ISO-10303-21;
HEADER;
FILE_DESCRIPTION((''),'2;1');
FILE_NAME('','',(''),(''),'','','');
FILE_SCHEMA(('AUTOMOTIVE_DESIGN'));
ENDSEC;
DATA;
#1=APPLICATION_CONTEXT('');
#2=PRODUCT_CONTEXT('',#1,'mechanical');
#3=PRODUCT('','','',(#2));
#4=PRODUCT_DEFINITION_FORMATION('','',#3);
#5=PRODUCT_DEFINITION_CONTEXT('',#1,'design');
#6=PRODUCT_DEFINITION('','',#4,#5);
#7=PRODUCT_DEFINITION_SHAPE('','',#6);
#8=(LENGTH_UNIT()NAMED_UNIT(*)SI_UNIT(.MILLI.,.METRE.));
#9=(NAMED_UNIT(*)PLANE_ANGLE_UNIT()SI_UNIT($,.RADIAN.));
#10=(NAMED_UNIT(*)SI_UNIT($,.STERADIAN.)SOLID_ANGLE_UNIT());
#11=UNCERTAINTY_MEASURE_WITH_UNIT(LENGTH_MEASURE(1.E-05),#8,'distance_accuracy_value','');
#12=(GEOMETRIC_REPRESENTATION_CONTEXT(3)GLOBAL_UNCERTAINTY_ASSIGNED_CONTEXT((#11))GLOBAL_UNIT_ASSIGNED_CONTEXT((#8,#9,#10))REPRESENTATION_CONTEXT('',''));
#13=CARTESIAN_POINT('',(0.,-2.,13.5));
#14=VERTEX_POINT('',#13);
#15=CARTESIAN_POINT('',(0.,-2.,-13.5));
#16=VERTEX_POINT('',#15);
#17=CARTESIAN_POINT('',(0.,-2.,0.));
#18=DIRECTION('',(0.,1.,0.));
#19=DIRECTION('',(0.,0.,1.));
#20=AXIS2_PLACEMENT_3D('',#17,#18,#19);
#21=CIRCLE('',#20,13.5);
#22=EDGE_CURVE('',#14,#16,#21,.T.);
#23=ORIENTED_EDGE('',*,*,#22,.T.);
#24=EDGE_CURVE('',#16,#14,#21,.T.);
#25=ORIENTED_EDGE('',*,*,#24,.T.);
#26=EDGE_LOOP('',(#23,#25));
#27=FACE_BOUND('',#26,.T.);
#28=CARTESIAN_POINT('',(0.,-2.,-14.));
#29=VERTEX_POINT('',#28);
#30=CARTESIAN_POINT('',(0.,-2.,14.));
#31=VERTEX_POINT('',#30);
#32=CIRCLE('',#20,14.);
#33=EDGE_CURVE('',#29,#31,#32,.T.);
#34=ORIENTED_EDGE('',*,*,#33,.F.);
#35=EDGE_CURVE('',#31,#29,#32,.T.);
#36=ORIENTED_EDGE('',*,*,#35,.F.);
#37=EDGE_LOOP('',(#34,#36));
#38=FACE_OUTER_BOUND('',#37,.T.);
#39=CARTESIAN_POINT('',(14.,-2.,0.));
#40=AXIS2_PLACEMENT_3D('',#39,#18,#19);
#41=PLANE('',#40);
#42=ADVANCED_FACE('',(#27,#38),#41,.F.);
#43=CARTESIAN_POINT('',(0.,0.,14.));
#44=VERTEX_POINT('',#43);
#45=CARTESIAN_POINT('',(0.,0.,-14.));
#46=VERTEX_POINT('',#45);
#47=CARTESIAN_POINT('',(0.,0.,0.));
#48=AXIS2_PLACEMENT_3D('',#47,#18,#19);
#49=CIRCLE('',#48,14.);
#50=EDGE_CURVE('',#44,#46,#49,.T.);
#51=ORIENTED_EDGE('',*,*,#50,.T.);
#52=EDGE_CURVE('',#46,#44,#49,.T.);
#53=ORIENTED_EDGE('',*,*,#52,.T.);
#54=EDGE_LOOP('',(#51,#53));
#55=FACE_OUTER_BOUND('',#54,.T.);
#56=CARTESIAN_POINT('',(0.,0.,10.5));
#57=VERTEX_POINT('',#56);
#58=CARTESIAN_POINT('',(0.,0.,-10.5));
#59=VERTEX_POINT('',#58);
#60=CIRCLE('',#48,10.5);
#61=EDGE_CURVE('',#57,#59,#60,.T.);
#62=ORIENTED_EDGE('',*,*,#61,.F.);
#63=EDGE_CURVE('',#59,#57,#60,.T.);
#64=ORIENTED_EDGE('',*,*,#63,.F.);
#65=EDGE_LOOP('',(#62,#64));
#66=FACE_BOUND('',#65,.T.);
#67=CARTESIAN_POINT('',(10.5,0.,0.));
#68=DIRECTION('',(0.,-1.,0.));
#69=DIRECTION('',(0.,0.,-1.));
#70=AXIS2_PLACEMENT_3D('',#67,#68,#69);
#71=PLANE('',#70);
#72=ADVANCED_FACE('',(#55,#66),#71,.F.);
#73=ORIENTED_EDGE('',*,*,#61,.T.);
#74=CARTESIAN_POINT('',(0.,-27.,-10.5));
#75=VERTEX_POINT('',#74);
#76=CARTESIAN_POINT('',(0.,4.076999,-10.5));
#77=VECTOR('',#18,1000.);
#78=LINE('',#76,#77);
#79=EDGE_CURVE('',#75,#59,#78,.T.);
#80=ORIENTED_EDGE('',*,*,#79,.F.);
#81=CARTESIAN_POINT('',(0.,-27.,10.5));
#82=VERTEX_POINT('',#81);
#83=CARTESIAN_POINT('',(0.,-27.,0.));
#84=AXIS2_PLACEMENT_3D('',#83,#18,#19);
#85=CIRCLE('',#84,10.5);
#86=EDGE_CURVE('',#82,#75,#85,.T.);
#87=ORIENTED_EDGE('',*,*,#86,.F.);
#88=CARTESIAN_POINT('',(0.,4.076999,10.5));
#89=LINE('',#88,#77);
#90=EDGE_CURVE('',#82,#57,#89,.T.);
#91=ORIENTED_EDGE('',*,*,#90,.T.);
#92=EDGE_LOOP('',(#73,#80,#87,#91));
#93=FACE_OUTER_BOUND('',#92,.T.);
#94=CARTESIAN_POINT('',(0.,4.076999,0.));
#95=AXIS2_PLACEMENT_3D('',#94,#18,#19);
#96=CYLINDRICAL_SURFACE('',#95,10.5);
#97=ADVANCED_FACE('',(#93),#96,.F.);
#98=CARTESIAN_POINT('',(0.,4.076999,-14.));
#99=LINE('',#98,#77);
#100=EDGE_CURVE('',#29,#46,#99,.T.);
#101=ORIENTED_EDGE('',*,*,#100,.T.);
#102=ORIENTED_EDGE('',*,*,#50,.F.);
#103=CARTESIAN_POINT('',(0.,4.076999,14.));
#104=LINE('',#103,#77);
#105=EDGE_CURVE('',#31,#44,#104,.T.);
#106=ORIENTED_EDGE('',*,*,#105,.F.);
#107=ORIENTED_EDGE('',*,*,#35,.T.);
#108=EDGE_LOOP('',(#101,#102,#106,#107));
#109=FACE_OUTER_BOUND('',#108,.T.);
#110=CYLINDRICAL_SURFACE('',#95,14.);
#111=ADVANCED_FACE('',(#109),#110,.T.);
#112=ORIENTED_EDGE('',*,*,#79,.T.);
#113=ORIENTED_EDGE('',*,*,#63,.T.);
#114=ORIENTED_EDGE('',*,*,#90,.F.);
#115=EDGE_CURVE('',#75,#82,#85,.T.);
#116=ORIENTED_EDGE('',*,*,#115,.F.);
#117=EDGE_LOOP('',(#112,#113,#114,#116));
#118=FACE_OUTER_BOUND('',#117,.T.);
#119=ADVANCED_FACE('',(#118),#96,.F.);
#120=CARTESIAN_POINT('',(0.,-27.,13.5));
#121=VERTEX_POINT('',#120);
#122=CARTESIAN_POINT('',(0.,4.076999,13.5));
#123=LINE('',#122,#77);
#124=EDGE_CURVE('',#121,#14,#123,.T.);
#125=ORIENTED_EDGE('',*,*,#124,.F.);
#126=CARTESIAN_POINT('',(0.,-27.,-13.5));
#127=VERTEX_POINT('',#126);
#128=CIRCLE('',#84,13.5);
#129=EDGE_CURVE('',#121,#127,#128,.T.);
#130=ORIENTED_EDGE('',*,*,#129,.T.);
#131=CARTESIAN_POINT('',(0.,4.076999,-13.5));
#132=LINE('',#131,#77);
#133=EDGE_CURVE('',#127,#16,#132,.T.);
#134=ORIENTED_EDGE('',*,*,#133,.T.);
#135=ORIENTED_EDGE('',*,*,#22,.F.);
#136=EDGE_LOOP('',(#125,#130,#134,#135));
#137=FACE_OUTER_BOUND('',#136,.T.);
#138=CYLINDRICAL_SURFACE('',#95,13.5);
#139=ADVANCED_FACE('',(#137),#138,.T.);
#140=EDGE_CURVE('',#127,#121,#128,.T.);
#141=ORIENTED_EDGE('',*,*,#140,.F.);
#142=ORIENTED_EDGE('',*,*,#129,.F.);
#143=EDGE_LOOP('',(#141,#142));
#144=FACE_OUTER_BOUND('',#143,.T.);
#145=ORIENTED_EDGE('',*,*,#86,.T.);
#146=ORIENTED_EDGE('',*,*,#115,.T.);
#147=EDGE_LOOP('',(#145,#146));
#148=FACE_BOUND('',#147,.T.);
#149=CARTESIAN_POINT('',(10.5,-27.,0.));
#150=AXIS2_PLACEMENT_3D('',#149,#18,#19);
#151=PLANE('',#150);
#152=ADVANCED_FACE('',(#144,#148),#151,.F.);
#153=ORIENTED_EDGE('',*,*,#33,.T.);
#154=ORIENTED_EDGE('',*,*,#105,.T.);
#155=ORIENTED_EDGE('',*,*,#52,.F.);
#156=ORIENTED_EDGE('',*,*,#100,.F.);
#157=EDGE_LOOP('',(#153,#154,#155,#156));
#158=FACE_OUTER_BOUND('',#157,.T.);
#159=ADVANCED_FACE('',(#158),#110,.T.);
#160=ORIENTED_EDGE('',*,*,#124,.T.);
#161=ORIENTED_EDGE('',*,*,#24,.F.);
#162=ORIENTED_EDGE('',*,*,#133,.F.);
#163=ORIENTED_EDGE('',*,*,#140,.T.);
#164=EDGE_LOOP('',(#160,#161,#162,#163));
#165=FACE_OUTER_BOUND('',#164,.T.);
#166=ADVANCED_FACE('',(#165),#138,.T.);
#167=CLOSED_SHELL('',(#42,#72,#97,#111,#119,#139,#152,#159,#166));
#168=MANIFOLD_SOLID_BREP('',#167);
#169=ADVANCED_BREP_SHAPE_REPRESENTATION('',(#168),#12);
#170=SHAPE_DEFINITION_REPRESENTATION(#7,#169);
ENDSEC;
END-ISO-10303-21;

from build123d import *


with BuildPart() as part:
    # 草图1 → 旋转1 (revolve)
    with BuildSketch(Plane.XY, mode=Mode.PRIVATE) as revolve_1_sk:
        Polygon((10.5, 0), (14, 0), (14, -2), (13.5, -2), (13.5, -27), (10.5, -27), align=None)
    revolve(revolve_1_sk.sketch.rotate(Axis((0, 4.076999107, 0), (0, -1, 0)), 90), axis=Axis((0, 4.076999107, 0), (0, -1, 0)))


solid = part.part
